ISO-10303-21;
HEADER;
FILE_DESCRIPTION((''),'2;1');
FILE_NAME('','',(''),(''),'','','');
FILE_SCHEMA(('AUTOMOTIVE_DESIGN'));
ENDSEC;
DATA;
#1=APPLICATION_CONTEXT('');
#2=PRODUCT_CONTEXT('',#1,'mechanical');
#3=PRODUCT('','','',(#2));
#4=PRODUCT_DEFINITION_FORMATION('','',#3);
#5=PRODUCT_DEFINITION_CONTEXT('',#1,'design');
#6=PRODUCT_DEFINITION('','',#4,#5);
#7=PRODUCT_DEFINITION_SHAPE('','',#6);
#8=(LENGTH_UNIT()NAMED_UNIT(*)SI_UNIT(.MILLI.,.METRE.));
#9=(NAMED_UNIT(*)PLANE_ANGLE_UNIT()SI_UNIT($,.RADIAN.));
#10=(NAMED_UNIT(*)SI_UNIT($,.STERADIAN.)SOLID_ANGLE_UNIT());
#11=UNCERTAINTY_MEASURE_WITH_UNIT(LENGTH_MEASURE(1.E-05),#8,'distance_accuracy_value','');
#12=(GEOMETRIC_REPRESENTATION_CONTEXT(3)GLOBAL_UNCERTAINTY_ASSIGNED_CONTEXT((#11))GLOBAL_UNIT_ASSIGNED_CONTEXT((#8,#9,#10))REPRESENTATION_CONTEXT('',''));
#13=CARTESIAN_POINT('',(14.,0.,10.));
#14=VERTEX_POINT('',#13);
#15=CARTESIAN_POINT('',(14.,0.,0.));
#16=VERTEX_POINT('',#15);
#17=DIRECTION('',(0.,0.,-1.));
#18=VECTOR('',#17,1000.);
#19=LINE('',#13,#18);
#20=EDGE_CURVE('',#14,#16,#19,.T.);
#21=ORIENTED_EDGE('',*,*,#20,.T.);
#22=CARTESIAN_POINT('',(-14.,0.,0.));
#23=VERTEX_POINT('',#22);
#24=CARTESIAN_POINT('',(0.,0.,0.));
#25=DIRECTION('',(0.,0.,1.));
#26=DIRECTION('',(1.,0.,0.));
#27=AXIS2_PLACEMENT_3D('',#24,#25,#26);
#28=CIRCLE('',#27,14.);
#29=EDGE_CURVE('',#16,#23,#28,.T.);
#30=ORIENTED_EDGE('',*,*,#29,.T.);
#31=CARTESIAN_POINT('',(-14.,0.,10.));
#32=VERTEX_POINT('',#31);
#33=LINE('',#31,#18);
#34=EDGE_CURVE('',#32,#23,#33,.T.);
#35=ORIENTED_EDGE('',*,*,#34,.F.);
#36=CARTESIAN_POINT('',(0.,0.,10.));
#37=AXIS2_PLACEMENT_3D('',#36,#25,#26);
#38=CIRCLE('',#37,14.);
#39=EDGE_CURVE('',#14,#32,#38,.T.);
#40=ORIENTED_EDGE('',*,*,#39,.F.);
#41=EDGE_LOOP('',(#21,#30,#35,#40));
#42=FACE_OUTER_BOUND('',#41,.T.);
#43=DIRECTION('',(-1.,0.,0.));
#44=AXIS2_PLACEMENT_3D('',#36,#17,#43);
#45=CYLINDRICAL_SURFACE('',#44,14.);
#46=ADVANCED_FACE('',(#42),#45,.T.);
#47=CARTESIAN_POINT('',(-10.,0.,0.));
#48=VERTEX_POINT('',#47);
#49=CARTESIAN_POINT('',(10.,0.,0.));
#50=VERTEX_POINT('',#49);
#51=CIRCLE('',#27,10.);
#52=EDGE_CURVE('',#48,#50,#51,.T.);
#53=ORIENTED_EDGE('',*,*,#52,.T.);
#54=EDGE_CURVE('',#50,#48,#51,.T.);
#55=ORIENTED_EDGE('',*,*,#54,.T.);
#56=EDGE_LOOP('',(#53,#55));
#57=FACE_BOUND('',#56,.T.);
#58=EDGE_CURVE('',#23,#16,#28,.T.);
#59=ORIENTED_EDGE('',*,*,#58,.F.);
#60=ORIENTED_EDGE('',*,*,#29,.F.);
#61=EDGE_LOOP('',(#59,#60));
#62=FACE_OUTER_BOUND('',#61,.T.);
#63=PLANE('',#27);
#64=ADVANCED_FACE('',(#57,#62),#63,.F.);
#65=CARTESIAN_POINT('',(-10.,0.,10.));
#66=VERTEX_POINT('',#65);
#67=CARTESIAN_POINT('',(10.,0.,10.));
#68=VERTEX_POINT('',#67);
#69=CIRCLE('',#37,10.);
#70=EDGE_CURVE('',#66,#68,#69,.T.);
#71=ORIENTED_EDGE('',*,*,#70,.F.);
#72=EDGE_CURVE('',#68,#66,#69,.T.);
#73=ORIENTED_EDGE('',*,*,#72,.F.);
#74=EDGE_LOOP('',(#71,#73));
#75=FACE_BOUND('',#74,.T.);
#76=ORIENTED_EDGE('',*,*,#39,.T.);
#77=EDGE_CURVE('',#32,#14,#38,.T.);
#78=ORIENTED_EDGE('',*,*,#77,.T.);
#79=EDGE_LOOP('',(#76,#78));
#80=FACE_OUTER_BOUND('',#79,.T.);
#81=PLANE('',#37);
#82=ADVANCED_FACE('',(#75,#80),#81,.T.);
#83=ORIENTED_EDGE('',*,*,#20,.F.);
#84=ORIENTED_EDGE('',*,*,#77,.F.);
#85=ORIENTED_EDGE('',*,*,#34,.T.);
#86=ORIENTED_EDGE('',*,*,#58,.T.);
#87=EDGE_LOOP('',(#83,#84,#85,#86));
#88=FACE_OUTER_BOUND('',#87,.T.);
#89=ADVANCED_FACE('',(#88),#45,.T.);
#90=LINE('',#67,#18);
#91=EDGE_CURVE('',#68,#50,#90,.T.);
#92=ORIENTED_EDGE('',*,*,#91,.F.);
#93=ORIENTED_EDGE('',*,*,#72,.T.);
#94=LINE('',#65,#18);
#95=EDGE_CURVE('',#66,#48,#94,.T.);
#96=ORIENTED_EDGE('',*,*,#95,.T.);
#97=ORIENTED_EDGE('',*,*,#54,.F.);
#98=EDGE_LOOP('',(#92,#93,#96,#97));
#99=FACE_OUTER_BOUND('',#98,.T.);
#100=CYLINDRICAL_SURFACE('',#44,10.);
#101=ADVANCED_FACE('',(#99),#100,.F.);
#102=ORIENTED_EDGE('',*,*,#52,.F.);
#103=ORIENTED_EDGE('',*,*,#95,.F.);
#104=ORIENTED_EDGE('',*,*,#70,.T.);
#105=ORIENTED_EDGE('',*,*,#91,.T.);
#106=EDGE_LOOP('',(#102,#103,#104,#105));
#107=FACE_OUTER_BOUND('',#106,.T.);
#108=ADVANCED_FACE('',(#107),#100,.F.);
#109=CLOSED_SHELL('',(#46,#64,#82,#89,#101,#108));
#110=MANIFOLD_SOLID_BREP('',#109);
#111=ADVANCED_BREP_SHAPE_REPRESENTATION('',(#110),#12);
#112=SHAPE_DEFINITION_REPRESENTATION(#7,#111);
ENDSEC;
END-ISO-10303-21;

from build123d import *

# Parameters (mm, degrees)
SKETCH_2_R      = 14
SKETCH_2_R_2    = 10
EXTRUDE_1_DEPTH = 10


with BuildPart() as part:
    # 草图2 → 凸台-拉伸1 (new body)
    with BuildSketch(Plane.XY):
        Circle(SKETCH_2_R)
        Circle(SKETCH_2_R_2, mode=Mode.SUBTRACT)
    extrude(amount=EXTRUDE_1_DEPTH)


solid = part.part
